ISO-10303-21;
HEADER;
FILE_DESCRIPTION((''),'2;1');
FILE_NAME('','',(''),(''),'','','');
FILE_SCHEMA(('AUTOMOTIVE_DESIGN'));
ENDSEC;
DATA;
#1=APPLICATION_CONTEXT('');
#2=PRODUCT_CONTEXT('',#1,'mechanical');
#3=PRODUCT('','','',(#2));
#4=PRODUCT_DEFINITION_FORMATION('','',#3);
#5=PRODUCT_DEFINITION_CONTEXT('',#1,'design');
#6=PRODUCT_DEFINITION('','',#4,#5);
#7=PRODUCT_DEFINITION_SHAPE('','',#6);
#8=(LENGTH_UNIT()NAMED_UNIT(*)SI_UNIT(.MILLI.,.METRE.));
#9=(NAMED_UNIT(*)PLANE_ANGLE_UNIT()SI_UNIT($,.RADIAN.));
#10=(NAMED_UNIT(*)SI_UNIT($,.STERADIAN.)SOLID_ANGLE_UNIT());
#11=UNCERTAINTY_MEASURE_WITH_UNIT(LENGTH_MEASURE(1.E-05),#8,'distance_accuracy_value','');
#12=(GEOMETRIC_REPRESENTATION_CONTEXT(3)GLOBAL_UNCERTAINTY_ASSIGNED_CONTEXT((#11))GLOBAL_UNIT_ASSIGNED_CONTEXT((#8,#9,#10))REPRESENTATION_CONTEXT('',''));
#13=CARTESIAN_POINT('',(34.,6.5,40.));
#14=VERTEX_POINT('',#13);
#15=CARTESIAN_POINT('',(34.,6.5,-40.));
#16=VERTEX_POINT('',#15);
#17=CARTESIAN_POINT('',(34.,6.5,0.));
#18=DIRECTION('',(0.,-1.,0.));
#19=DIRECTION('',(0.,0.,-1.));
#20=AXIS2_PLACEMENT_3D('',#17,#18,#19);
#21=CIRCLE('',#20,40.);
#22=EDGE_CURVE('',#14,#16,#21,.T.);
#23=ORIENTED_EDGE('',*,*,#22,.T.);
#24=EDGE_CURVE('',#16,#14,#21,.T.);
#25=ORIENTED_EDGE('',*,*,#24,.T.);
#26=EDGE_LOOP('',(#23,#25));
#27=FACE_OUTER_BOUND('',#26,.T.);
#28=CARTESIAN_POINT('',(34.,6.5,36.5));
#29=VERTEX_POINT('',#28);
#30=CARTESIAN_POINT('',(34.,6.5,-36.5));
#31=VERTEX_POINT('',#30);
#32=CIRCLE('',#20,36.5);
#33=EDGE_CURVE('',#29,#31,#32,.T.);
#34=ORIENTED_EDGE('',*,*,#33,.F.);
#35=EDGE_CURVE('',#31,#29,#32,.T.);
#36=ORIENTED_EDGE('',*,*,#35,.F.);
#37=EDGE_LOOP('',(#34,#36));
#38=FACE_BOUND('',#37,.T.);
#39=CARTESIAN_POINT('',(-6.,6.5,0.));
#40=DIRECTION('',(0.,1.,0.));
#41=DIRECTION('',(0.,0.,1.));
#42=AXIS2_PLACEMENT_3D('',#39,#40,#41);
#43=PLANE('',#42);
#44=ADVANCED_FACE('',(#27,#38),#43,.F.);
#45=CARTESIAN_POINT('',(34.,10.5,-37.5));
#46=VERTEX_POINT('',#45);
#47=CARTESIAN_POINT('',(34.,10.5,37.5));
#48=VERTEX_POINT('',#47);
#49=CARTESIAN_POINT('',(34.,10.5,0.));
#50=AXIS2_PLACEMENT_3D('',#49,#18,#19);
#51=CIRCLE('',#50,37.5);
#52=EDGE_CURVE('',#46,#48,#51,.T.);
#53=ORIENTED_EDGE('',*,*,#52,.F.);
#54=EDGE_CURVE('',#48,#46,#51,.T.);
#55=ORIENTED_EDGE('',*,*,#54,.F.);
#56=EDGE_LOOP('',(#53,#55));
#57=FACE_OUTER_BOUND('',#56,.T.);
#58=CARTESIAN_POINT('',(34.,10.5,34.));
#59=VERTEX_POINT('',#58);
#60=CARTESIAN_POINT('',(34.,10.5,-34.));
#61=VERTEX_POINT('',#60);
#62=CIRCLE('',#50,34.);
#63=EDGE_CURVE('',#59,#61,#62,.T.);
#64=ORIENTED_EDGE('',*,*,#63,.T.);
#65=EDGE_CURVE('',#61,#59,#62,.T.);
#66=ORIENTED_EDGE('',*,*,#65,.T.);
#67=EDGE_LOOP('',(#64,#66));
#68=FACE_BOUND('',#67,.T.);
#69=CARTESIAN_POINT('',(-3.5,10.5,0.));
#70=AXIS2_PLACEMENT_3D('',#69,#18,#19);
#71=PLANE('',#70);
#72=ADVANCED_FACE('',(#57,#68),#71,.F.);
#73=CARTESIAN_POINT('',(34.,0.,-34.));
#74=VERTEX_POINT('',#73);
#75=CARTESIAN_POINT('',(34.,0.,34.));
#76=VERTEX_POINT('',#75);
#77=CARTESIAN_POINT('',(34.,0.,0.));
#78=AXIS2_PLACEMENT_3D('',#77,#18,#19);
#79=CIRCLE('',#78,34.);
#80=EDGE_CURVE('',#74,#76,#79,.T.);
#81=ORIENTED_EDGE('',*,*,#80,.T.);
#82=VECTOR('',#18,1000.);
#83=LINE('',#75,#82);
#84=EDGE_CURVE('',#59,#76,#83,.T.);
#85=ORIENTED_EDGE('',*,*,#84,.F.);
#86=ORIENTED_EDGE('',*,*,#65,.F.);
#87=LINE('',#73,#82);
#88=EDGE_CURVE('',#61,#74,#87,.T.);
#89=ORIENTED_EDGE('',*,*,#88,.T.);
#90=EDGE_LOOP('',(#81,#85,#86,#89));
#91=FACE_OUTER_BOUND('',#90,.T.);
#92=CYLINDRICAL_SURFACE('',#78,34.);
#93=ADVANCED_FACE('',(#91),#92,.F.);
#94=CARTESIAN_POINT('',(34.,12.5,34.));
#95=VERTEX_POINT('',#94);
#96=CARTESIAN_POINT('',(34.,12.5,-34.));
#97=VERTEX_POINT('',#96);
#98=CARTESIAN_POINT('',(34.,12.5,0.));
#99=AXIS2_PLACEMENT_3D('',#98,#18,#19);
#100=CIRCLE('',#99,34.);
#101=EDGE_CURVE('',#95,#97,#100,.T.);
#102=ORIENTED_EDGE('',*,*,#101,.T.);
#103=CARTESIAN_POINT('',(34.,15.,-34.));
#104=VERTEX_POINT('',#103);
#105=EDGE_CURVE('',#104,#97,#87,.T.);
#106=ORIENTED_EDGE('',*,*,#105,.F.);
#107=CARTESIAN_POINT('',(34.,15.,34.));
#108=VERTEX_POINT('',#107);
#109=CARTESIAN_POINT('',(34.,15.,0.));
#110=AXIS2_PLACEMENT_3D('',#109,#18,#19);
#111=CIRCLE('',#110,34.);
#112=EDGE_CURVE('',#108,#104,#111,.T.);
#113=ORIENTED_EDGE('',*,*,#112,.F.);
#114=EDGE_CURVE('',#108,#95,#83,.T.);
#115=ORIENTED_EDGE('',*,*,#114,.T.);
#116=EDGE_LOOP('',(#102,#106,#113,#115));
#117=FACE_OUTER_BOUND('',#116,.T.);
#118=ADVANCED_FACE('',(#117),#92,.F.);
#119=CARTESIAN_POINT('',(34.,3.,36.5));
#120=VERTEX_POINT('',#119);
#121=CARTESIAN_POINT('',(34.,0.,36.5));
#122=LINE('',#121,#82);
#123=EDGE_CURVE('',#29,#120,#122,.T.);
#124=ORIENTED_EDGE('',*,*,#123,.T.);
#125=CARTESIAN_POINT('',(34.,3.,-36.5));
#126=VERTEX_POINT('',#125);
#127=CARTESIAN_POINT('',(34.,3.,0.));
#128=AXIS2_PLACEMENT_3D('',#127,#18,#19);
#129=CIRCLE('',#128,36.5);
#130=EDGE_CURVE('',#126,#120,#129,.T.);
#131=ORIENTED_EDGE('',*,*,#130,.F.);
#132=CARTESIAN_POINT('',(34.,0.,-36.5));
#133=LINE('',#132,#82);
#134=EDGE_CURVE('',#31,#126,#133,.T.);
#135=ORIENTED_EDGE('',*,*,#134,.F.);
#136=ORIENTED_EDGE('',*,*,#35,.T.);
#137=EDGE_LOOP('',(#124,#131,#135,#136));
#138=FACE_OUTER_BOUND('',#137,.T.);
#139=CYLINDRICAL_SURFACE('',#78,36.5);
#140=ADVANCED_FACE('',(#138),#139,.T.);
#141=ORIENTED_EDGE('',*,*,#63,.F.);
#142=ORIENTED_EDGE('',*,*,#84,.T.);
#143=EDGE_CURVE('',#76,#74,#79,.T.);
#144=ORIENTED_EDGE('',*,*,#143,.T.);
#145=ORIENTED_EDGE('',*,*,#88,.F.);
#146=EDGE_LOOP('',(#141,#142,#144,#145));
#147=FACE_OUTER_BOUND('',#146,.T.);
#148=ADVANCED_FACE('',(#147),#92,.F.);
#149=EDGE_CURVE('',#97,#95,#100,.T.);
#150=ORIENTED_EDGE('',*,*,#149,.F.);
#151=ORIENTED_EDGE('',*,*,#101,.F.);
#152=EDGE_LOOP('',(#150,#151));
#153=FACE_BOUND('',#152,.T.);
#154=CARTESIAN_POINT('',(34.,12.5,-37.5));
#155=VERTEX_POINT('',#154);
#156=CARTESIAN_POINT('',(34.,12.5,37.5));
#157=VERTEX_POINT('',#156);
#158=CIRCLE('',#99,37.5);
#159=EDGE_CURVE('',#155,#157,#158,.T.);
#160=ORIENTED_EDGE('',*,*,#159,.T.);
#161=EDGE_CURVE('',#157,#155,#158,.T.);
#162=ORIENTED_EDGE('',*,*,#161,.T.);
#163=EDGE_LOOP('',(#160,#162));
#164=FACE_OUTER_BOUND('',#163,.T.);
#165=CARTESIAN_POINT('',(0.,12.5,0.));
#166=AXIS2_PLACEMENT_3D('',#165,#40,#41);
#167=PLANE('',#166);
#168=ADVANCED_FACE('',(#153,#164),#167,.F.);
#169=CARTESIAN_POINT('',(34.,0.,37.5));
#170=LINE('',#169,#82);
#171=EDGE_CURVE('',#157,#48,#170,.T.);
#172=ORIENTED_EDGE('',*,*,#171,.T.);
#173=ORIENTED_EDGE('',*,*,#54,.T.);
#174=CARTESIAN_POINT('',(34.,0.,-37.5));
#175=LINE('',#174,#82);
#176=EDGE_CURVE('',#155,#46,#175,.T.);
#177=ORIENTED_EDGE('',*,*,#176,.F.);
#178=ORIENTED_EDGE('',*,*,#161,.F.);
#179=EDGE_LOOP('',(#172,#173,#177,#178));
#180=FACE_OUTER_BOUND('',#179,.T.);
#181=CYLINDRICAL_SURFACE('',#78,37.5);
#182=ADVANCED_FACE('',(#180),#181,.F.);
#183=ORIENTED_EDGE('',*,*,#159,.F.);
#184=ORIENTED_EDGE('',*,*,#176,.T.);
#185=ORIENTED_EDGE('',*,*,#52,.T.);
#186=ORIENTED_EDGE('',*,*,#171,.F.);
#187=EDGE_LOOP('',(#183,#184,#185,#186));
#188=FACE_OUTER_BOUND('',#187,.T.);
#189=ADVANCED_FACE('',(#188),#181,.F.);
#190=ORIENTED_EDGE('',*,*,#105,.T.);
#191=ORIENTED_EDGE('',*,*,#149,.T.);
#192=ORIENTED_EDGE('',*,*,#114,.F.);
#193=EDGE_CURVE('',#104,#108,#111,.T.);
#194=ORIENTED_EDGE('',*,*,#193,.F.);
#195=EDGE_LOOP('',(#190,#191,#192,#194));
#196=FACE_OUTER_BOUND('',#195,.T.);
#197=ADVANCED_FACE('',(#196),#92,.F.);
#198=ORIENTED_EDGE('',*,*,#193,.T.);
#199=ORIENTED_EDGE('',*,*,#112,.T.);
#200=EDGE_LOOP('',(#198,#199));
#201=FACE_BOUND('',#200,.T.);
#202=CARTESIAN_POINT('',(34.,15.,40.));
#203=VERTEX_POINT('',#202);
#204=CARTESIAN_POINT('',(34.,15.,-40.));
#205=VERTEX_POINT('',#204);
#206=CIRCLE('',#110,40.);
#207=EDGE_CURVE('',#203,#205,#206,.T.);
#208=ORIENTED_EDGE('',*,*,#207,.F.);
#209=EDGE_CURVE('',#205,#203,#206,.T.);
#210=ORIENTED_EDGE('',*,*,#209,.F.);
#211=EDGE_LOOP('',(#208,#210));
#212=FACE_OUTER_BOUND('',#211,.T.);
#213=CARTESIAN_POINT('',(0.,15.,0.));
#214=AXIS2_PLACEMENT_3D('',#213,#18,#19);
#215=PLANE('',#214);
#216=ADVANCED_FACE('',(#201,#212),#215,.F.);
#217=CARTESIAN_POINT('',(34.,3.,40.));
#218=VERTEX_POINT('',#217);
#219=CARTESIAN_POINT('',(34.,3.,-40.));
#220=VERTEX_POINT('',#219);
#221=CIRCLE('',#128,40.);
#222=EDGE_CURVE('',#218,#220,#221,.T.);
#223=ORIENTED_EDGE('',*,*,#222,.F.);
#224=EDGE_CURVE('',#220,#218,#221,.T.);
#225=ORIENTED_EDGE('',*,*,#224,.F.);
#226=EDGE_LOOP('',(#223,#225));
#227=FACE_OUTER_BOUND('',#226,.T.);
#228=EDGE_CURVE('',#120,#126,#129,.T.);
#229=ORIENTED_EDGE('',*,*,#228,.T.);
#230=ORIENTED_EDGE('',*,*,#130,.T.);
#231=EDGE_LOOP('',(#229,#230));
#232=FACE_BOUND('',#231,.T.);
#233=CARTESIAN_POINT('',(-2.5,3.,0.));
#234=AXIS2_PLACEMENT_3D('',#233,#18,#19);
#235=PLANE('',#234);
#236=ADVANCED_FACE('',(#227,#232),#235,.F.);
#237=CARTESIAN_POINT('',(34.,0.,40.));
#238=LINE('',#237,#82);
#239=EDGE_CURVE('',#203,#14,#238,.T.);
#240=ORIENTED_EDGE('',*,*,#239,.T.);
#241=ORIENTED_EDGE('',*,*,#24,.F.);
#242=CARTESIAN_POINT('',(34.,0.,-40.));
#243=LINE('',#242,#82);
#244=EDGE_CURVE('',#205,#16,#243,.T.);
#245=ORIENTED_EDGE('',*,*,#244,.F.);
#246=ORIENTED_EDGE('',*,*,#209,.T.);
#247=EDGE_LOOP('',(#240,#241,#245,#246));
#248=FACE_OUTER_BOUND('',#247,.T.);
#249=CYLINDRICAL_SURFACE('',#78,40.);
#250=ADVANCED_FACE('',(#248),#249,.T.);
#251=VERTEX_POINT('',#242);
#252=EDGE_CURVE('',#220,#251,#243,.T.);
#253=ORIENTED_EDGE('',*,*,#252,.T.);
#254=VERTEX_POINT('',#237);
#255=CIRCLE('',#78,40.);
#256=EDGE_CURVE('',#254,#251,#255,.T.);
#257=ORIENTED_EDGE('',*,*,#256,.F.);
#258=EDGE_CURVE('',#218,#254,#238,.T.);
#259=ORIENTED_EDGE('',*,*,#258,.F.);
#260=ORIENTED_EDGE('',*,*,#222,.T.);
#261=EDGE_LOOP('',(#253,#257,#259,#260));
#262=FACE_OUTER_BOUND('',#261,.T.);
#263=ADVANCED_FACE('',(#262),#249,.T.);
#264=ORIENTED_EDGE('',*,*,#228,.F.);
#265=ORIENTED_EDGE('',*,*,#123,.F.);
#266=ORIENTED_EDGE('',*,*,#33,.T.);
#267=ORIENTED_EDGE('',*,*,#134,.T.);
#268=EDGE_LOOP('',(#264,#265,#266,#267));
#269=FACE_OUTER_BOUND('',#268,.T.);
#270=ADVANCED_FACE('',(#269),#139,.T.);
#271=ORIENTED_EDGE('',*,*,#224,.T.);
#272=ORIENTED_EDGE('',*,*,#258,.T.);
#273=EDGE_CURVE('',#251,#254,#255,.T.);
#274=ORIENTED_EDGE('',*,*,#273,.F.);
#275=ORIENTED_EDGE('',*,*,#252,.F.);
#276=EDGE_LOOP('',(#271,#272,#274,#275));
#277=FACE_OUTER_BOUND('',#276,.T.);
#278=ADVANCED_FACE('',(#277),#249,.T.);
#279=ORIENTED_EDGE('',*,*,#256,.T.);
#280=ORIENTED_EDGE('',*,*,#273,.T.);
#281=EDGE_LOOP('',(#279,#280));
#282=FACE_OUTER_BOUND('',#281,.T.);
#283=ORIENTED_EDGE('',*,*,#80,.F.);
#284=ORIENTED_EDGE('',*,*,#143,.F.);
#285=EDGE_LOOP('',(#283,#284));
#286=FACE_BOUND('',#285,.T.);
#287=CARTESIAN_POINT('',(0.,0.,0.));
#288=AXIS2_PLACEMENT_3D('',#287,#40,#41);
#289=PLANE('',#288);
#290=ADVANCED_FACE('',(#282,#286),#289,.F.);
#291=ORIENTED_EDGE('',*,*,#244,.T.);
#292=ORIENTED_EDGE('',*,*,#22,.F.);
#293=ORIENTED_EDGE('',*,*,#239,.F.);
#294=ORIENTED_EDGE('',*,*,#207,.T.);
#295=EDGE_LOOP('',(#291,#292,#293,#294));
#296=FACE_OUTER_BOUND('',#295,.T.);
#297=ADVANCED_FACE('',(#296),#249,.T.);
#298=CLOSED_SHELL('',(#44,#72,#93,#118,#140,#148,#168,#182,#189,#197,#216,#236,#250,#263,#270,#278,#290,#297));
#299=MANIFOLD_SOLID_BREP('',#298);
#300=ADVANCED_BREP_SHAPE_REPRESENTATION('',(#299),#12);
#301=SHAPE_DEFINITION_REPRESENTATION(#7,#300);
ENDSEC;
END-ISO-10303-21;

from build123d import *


with BuildPart() as part:
    # 草图1 → 旋转1 (revolve)
    with BuildSketch(Plane.XY, mode=Mode.PRIVATE) as revolve_1_sk:
        Polygon((0, 0), (-6, 0), (-6, 3), (-2.5, 3), (-2.5, 6.5), (-6, 6.5), (-6, 15), (0, 15), (0, 12.5), (-3.5, 12.5), (-3.5, 10.5), (0, 10.5), align=None)
    revolve(revolve_1_sk.sketch.rotate(Axis((34, 0, 0), (0, 1, 0)), 270), axis=Axis((34, 0, 0), (0, 1, 0)))


solid = part.part
